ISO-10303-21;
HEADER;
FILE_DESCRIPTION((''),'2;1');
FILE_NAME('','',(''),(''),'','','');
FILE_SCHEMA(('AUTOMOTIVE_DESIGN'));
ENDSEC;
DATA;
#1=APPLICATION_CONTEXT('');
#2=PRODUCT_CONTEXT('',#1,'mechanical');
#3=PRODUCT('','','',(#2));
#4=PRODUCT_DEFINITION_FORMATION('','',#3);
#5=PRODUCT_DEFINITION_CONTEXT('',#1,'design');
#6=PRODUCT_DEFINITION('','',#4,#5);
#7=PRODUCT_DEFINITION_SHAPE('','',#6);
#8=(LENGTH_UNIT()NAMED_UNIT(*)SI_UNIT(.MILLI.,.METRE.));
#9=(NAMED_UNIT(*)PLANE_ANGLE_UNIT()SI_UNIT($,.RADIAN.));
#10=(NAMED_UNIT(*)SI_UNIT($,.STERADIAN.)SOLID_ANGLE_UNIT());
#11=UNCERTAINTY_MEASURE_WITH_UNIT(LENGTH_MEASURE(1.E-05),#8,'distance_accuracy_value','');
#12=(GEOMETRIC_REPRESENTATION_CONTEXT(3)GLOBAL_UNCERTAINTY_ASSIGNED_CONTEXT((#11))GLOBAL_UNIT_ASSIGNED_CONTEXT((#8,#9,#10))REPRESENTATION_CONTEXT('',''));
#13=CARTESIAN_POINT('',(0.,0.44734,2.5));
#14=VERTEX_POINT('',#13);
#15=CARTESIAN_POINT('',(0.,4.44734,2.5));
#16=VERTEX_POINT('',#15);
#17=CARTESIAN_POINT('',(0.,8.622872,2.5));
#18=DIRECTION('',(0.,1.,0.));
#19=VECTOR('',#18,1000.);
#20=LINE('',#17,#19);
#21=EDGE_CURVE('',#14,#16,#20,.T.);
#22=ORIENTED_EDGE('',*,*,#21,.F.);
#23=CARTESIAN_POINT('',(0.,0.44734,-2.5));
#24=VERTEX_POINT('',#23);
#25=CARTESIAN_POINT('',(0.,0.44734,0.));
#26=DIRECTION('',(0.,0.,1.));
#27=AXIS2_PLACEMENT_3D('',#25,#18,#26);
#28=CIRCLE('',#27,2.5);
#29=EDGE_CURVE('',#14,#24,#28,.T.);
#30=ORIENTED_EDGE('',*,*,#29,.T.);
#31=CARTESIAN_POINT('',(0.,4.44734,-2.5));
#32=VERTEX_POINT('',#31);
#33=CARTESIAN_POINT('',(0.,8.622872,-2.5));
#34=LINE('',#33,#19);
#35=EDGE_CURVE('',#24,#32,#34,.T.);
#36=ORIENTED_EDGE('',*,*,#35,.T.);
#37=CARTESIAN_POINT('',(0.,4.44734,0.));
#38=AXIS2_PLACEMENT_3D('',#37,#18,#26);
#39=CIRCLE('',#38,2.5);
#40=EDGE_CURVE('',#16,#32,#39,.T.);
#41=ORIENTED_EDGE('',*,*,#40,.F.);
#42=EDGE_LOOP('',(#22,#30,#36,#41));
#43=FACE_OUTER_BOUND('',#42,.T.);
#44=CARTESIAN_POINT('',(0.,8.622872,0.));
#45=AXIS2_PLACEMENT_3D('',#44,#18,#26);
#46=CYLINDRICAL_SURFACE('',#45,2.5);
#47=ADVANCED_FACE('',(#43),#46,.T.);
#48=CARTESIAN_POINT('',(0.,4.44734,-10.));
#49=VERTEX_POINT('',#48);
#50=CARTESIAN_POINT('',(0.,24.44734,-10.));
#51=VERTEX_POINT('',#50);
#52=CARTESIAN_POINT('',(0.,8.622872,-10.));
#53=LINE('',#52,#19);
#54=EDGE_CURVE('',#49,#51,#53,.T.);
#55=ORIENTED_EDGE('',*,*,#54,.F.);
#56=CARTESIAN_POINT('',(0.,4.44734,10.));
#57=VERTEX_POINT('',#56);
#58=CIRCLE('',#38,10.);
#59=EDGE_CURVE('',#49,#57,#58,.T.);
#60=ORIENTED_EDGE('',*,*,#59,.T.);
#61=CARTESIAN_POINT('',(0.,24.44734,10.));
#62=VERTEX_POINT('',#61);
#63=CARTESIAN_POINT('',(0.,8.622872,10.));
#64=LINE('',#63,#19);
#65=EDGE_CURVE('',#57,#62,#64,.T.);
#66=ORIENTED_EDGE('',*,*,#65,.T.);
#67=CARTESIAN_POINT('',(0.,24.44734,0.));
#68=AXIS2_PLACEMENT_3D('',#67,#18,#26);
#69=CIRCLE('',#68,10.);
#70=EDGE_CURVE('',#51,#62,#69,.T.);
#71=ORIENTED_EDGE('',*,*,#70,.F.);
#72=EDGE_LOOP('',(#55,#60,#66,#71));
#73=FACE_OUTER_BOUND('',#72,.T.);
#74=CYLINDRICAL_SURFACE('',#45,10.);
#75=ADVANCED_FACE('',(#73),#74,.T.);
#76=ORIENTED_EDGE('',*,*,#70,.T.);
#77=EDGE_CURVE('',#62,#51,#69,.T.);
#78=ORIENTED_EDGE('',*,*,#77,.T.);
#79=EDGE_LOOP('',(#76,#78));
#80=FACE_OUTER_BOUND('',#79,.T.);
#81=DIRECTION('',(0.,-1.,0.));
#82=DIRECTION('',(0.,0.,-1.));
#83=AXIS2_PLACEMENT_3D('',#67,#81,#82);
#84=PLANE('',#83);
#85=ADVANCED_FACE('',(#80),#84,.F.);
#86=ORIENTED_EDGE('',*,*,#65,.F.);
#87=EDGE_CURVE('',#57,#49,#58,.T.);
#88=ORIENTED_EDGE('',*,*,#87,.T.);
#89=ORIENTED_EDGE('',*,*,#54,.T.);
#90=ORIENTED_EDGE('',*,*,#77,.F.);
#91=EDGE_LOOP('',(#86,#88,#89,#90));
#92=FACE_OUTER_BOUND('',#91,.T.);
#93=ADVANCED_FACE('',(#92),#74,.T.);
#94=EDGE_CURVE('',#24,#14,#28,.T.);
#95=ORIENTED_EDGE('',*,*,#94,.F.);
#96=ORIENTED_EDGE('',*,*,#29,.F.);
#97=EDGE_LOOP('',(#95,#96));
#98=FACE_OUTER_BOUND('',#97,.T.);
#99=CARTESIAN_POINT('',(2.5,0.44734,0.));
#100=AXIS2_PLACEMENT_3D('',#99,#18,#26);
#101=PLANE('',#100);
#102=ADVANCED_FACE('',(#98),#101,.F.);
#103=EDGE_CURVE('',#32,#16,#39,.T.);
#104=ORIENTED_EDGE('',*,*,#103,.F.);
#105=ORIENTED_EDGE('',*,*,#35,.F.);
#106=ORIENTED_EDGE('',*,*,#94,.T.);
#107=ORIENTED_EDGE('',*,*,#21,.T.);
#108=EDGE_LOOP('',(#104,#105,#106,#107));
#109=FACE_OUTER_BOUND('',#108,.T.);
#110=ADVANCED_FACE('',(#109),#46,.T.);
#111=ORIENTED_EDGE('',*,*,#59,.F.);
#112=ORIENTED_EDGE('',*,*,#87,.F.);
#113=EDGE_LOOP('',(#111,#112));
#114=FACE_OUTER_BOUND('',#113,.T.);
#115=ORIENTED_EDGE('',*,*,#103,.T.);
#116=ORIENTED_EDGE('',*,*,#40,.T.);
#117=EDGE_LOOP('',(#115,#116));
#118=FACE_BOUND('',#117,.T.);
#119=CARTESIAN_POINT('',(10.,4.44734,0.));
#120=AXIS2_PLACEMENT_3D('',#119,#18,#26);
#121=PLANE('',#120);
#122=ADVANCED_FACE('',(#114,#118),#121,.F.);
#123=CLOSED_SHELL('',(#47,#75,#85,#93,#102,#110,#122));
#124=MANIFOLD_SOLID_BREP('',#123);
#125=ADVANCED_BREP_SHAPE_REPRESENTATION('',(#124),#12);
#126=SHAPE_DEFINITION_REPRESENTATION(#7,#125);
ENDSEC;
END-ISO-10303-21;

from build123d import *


with BuildPart() as part:
    # Sketch1 → Revolve1 (revolve)
    with BuildSketch(Plane.XY, mode=Mode.PRIVATE) as revolve1_sk:
        Polygon((0, 24.447340426), (10, 24.447340426), (10, 4.447340426), (2.5, 4.447340426), (2.5, 0.447340426), (0, 0.447340426), align=None)
    revolve(revolve1_sk.sketch.rotate(Axis((0, 8.62287234, 0), (0, -1, 0)), 90), axis=Axis((0, 8.62287234, 0), (0, -1, 0)))


solid = part.part
